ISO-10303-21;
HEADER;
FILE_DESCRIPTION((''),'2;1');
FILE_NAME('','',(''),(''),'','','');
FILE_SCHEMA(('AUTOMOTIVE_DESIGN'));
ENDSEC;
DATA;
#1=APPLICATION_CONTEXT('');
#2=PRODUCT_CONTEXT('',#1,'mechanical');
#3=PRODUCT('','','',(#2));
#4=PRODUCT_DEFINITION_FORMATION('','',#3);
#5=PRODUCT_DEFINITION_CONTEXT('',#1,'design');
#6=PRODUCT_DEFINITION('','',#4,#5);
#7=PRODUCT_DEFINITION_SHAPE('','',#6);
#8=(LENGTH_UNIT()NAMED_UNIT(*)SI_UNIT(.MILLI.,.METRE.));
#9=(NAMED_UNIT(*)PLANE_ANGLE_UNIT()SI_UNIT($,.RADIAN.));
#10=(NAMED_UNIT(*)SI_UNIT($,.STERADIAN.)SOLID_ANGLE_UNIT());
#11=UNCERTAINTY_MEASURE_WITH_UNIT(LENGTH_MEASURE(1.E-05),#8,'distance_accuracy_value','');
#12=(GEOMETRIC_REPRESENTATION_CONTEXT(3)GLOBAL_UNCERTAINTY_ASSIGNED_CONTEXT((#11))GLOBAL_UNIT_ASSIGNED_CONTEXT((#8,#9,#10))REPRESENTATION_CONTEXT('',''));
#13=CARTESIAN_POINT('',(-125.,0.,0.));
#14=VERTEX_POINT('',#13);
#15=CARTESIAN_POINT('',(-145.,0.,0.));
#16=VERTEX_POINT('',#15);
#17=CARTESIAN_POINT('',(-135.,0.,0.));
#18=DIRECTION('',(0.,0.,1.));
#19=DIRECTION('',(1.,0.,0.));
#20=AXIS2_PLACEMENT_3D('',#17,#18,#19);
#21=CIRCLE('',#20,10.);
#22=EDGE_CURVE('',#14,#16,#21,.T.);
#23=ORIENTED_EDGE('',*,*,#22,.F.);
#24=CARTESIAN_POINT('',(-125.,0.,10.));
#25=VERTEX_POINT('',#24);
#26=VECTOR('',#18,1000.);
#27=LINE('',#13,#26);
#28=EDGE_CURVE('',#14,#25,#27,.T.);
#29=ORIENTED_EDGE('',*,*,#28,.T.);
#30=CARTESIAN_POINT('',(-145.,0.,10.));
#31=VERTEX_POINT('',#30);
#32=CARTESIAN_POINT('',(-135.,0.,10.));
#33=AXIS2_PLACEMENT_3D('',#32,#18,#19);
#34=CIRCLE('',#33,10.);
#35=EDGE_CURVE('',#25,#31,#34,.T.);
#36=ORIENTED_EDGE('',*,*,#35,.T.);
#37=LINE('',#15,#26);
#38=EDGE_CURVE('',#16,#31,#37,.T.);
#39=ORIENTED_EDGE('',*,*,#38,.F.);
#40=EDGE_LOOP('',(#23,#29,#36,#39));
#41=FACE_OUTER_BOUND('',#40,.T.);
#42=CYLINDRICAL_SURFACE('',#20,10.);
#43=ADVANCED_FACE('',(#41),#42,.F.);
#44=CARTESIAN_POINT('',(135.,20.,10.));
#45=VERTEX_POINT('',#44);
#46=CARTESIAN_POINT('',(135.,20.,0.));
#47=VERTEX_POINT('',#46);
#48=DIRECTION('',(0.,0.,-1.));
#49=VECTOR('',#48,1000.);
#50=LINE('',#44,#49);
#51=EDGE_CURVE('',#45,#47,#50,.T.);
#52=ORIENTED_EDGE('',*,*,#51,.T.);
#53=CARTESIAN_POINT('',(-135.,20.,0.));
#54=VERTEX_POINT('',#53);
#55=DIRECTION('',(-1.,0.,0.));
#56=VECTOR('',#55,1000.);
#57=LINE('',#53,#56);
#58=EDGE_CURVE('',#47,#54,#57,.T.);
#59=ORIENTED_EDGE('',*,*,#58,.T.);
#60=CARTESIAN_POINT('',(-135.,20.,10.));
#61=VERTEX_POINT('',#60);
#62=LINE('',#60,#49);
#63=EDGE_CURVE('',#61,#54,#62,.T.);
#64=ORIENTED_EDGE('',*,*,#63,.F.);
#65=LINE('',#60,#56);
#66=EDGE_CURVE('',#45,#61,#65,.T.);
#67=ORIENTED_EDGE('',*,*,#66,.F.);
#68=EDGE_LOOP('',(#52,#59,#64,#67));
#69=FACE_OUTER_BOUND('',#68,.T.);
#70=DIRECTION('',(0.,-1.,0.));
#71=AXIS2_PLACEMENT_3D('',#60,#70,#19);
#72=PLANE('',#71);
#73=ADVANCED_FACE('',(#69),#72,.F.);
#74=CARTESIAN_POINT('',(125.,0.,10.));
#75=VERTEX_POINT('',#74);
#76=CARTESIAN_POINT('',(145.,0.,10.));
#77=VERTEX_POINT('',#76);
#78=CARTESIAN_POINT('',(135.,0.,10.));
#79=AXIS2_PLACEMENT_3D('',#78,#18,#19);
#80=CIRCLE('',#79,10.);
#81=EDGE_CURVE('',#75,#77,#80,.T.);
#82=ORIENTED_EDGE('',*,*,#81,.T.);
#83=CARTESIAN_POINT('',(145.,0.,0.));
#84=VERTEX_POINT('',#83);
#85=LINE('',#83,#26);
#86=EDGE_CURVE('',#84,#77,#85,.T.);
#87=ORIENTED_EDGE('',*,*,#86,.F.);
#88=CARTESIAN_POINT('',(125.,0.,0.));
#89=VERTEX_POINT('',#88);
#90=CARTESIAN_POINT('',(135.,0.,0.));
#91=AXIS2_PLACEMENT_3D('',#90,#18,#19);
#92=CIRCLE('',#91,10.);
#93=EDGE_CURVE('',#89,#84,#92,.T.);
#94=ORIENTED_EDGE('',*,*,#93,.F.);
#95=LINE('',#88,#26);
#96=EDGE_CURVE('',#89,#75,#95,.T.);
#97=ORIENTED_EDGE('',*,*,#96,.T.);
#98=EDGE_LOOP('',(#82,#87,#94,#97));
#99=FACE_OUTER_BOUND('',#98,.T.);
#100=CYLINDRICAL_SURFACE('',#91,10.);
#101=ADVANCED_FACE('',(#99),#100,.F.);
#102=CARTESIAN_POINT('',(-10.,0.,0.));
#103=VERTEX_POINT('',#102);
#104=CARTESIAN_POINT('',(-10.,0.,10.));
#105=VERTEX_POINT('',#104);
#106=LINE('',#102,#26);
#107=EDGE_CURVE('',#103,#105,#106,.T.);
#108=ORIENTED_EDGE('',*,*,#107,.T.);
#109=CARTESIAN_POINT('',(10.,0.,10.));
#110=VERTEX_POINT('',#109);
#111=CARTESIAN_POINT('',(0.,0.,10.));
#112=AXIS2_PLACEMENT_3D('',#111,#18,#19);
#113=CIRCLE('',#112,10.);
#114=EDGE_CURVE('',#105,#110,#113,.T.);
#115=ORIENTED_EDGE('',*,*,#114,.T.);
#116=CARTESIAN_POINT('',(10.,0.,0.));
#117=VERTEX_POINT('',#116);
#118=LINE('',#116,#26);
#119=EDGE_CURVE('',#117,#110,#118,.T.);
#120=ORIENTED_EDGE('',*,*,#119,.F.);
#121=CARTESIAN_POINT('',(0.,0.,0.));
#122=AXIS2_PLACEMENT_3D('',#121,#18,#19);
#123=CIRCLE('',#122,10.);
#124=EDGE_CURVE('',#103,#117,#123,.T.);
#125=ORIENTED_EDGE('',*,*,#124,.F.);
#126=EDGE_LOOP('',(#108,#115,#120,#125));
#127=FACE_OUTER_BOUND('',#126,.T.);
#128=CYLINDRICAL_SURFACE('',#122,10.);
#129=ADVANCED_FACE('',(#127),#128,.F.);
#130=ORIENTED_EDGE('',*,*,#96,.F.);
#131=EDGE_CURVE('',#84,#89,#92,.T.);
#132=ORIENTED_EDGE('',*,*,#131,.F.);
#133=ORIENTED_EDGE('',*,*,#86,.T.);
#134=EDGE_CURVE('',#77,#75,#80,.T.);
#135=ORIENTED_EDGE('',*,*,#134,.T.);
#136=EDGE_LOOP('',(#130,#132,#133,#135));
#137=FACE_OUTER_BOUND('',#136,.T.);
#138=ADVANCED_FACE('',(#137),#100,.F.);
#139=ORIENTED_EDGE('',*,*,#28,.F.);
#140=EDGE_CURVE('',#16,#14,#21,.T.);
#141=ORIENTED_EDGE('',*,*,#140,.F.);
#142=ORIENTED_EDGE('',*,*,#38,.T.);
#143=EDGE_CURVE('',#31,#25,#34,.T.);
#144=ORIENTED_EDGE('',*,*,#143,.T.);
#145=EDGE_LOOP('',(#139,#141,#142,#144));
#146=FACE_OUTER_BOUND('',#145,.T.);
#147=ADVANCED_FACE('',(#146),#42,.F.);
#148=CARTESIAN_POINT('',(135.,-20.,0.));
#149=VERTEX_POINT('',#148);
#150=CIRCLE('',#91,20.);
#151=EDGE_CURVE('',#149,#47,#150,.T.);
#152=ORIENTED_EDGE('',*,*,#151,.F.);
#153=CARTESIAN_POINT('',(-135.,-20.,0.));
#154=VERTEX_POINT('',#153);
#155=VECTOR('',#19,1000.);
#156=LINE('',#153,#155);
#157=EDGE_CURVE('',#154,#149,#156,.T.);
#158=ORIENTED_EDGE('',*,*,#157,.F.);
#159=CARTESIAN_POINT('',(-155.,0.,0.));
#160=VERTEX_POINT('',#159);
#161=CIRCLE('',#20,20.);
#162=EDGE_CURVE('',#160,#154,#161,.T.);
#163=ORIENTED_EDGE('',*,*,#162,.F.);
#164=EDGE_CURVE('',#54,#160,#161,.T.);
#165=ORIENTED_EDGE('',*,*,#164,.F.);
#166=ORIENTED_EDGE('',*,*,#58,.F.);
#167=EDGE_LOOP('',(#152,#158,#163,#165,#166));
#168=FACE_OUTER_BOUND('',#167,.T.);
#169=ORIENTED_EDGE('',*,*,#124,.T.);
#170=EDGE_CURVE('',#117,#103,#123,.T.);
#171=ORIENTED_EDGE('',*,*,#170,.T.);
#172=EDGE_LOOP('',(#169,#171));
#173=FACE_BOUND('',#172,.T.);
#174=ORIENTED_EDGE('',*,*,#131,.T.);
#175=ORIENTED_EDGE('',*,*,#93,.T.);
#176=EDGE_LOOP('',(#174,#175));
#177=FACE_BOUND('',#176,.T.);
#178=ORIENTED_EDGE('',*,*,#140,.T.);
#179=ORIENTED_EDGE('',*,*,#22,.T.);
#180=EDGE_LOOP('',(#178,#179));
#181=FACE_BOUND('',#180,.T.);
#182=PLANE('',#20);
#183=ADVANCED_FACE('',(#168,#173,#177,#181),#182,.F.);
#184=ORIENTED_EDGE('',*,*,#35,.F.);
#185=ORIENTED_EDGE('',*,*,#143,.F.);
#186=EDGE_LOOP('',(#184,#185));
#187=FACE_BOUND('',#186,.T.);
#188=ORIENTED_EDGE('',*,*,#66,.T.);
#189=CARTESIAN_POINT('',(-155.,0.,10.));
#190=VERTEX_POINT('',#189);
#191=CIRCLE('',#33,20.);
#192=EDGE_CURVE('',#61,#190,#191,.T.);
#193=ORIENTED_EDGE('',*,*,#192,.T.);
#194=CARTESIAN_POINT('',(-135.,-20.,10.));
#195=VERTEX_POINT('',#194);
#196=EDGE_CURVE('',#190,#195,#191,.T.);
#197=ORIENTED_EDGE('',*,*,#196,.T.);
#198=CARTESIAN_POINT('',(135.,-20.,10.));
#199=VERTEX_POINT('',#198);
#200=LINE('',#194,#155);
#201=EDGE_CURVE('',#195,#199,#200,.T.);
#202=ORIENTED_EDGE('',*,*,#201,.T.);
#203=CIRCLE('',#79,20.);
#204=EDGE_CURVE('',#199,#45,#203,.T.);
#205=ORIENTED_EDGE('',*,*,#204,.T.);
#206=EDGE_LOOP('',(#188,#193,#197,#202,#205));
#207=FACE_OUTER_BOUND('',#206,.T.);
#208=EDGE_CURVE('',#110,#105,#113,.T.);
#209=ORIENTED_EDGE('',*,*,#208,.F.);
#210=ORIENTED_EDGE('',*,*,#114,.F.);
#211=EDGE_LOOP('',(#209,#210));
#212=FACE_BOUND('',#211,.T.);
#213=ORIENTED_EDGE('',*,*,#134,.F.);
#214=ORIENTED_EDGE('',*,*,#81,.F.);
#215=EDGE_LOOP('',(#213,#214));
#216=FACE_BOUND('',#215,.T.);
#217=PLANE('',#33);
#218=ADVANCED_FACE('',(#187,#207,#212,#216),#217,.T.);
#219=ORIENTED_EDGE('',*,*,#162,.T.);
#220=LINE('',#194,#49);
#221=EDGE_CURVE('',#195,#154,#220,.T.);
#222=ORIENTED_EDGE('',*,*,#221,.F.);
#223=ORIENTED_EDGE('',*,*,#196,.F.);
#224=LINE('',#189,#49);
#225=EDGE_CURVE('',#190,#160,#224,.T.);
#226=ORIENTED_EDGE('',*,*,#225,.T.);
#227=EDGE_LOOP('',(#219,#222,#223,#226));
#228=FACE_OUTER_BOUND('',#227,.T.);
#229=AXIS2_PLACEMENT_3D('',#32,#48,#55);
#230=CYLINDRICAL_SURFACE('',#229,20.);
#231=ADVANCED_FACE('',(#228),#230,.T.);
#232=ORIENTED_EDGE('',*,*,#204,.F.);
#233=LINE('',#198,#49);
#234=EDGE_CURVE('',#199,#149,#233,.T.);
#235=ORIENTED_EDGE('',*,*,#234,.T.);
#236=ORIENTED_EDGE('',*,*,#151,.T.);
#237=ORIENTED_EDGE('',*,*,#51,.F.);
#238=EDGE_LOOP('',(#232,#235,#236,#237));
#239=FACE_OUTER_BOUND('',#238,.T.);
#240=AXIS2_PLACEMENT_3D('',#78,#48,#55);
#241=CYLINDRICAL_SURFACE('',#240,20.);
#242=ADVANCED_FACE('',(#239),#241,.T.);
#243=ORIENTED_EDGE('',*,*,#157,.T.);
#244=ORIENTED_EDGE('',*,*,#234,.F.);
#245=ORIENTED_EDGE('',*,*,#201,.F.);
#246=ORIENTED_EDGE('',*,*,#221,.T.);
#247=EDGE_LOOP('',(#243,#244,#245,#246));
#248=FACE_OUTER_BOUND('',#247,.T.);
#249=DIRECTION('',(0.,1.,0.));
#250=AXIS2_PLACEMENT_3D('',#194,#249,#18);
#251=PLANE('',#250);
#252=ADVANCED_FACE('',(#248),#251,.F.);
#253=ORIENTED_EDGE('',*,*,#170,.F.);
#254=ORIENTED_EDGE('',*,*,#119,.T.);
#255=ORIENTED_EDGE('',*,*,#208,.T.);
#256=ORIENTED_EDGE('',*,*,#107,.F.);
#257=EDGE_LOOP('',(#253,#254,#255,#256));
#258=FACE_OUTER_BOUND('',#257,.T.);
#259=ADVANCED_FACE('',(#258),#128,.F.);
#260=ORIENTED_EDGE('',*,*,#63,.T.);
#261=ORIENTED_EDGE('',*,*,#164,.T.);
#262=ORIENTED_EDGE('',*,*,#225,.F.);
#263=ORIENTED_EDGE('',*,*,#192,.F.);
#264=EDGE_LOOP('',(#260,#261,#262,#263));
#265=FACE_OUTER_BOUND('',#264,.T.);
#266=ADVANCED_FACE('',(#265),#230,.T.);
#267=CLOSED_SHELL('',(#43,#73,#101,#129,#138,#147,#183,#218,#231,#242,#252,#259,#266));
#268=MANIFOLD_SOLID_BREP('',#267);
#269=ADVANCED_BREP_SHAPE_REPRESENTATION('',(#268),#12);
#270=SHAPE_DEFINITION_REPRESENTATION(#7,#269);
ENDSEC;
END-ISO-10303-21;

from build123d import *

# Parameters (mm, degrees)
BOSS_EXTRUDE1_DEPTH = 10
SKETCH2_R           = 10
CUT_EXTRUDE1_DEPTH  = 157.604597634
SKETCH3_R           = 10
CUT_EXTRUDE2_DEPTH  = 10


with BuildPart() as part:
    # Sketch1 → Boss-Extrude1 (new body)
    with BuildSketch(Plane.XY):
        with BuildLine():
            Line((-135, 20), (135, 20))
            ThreePointArc((135, 20), (155, 0), (135, -20))
            Line((135, -20), (-135, -20))
            ThreePointArc((-135, -20), (-155, 0), (-135, 20))
        make_face()
    extrude(amount=BOSS_EXTRUDE1_DEPTH)

    # Sketch2 → Cut-Extrude1 (cut, through all)
    with BuildSketch(Plane.XY.offset(10)):
        with Locations((-135, 0)):
            Circle(SKETCH2_R)
        with Locations((135, 0)):
            Circle(SKETCH2_R)
    extrude(amount=-CUT_EXTRUDE1_DEPTH, mode=Mode.SUBTRACT)

    # Sketch3 → Cut-Extrude2 (cut)
    with BuildSketch(Plane.XY.offset(10)):
        Circle(SKETCH3_R)
    extrude(amount=-CUT_EXTRUDE2_DEPTH, mode=Mode.SUBTRACT)


solid = part.part
